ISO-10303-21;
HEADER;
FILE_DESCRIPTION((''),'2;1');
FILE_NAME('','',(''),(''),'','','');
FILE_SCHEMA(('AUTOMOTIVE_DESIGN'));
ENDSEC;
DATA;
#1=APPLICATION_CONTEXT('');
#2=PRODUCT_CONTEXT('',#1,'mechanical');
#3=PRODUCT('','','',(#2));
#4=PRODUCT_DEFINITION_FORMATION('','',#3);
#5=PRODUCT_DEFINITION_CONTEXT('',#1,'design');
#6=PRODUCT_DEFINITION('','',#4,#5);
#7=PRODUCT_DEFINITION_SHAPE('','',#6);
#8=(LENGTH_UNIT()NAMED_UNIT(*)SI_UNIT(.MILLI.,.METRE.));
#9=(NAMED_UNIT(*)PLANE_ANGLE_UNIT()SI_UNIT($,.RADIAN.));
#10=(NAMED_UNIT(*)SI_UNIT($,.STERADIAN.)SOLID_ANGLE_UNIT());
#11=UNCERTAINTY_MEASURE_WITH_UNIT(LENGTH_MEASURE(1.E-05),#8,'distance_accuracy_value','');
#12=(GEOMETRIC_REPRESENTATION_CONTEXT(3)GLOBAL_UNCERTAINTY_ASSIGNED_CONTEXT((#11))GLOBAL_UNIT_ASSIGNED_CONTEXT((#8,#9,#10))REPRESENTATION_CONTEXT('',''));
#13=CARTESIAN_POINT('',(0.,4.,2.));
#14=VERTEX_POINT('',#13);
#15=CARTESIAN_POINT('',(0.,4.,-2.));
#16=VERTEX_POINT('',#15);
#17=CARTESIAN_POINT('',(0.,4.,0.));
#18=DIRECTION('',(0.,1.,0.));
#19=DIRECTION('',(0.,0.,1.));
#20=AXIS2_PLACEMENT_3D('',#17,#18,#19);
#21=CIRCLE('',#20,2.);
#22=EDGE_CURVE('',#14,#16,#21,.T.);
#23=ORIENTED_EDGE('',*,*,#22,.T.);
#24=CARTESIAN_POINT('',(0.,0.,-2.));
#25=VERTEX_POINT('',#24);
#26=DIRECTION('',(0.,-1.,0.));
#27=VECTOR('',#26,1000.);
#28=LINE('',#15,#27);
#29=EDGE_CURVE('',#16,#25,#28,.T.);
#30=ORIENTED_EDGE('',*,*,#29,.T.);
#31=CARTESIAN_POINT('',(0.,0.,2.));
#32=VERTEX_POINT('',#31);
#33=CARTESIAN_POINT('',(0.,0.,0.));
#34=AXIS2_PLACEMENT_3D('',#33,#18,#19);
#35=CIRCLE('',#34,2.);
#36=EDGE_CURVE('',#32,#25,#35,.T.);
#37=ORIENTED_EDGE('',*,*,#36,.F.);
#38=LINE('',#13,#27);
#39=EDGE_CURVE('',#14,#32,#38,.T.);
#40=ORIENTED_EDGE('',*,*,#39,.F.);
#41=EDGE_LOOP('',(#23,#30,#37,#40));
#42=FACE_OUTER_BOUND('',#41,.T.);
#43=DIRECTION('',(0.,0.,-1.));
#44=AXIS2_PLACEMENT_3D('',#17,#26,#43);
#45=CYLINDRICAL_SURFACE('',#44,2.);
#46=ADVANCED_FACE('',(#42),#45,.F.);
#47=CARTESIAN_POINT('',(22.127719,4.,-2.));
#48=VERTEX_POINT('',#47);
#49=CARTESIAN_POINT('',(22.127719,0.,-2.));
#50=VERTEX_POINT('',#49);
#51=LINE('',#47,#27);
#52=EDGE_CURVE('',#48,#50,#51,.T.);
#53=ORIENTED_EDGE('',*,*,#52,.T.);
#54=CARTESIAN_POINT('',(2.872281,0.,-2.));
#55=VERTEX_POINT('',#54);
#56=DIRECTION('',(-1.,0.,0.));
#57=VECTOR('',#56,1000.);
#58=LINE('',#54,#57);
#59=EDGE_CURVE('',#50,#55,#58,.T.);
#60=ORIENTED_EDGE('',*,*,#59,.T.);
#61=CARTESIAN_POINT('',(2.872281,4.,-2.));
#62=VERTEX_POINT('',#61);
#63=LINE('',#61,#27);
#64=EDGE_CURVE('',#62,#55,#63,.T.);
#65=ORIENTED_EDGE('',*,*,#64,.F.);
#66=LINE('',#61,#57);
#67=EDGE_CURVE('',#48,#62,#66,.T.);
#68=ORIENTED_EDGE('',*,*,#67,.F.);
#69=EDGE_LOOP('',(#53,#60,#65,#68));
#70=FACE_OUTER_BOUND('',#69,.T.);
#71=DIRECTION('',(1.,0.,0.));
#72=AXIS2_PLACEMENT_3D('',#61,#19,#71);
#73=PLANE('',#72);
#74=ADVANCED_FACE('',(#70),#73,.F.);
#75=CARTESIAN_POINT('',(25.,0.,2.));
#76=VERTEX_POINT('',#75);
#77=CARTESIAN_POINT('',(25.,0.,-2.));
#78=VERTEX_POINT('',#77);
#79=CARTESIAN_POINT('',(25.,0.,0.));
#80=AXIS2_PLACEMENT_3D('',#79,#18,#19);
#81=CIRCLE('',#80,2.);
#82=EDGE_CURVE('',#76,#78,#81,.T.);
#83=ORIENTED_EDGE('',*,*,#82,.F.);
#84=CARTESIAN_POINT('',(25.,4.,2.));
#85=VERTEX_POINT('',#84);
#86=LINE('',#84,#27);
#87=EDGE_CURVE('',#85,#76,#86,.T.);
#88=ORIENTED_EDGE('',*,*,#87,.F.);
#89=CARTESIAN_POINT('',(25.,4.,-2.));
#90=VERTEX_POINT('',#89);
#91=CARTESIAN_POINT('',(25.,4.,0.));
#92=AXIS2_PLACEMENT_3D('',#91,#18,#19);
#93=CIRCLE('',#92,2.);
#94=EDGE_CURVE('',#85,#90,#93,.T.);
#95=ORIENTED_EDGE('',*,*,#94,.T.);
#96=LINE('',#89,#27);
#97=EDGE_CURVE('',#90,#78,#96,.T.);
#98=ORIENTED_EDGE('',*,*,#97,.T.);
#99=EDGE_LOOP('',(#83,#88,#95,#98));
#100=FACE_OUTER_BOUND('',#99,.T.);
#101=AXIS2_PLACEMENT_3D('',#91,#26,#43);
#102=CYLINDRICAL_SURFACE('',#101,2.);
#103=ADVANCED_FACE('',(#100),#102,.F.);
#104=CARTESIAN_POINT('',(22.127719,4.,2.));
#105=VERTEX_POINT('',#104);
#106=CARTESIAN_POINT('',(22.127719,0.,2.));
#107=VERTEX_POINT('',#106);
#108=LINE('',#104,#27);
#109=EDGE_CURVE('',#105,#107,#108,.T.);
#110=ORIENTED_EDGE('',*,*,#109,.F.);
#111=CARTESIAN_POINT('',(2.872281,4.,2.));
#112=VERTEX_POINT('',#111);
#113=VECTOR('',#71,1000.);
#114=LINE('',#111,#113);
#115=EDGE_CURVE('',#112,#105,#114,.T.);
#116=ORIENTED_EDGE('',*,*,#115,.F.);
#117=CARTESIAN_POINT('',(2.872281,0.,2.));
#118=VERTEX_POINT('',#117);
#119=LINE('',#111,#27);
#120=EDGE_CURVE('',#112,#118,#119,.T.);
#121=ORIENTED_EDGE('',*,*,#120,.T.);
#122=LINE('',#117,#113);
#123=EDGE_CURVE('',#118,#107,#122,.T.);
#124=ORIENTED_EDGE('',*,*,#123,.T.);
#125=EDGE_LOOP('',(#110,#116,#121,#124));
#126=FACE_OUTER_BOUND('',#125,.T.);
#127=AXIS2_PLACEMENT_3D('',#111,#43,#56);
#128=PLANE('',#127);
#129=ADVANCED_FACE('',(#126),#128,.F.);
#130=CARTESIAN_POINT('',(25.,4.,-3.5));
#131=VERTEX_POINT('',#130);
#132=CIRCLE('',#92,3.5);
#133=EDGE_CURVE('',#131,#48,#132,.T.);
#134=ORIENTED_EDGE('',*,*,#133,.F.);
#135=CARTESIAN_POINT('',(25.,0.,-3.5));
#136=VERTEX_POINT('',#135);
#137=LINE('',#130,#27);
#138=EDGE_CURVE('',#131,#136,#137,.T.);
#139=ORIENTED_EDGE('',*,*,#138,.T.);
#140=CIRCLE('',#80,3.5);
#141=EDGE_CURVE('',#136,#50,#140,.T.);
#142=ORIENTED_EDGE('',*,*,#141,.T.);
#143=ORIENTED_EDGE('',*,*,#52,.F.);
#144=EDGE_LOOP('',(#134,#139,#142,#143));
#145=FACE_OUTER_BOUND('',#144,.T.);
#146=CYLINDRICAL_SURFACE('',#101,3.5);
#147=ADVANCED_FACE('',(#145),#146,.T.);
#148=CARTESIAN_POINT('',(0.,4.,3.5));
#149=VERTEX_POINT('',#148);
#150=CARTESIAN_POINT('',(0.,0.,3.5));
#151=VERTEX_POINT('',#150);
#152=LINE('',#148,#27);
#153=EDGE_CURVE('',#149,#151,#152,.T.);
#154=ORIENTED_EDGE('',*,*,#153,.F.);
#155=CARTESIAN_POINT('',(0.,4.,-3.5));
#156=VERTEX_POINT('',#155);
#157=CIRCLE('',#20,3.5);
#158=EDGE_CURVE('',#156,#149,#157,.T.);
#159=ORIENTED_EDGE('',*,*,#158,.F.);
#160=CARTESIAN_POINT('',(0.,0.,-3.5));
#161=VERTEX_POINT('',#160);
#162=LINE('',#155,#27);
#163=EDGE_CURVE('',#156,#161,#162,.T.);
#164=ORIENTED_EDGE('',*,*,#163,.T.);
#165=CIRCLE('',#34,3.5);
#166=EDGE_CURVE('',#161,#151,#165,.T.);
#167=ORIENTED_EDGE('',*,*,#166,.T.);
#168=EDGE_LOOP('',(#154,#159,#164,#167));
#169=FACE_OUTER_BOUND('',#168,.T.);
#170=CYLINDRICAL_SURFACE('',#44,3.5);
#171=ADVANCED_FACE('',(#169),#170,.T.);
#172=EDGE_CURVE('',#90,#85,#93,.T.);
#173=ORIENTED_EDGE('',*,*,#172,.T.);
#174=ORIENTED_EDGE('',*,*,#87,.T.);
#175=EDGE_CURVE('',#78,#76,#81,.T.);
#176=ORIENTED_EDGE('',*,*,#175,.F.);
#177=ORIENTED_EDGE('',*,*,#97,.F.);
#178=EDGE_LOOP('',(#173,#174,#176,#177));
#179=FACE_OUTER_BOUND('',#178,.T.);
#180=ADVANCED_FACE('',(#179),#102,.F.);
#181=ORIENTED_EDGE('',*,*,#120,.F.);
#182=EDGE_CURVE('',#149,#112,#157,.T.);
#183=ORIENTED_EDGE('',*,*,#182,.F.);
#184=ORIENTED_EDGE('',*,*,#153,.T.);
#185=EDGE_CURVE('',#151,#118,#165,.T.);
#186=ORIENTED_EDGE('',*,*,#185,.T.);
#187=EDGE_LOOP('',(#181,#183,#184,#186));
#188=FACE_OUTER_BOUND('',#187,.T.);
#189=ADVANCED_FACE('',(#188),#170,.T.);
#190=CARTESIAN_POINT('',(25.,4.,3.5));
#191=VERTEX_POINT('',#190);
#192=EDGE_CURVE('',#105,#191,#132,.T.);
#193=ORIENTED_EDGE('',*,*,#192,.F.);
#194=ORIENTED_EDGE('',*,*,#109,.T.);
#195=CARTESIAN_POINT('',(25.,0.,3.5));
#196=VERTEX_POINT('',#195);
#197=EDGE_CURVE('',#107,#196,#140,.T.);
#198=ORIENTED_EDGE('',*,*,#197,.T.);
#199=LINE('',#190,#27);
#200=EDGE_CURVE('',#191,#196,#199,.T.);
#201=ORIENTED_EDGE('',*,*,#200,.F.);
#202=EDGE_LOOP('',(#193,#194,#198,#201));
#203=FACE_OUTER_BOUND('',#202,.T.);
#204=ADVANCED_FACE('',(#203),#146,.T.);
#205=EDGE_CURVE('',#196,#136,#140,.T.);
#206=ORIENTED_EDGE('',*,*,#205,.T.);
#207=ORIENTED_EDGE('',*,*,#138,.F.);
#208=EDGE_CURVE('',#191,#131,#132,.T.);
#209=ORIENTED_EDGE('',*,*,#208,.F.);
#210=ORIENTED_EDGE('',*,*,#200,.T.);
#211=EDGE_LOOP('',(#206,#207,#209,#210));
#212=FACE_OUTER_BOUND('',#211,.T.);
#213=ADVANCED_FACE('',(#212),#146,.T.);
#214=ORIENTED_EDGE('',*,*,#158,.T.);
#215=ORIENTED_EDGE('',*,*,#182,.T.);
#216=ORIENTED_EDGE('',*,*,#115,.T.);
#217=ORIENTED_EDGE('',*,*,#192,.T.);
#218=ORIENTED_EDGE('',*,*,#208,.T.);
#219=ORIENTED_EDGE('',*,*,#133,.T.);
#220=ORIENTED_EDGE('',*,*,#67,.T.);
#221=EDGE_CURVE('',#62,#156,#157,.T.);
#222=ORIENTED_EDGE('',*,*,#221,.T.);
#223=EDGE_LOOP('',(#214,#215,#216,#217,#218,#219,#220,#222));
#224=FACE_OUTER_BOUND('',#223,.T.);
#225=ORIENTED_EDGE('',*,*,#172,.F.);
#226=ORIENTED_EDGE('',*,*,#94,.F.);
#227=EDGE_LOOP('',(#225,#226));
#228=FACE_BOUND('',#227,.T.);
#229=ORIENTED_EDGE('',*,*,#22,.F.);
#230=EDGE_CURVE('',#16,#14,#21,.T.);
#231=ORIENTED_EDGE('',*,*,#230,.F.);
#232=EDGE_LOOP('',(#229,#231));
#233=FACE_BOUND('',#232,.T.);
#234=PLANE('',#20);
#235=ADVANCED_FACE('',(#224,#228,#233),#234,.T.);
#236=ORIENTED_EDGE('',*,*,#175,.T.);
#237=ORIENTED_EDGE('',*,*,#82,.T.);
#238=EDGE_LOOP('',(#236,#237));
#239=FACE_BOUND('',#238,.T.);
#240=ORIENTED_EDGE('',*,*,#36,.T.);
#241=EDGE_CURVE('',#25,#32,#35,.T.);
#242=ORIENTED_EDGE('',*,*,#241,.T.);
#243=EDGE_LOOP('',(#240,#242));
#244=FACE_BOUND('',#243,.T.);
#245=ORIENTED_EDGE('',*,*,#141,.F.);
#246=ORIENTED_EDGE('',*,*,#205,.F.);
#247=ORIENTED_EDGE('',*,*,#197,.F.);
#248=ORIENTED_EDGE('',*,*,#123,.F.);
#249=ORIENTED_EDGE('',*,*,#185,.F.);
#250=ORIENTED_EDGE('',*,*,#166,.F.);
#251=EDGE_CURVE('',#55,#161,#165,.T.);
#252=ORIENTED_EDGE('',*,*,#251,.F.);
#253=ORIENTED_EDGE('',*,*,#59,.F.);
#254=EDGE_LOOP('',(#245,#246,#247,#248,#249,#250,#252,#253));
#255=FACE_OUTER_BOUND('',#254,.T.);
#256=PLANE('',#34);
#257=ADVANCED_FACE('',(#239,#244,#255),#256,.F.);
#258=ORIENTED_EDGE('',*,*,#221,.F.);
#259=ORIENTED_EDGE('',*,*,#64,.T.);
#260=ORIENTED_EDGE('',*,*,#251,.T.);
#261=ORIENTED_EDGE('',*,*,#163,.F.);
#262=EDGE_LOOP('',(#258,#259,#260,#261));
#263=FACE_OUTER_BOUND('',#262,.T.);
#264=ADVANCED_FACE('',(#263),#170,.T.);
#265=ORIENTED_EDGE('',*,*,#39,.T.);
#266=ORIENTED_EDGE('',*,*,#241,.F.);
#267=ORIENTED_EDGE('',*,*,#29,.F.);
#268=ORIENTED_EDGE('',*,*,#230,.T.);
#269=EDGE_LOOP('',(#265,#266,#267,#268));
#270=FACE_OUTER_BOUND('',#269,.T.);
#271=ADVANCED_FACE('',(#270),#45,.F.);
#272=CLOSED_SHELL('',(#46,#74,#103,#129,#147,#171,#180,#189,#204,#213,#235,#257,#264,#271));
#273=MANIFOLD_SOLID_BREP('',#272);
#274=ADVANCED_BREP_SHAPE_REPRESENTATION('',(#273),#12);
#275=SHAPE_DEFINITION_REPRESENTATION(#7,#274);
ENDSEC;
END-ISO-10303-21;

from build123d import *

# Parameters (mm, degrees)
SKETCH1_R           = 4
BOSS_EXTRUDE1_DEPTH = 8
SCALE1_SCALE        = 0.5


with BuildPart() as part:
    # Sketch1 → Boss-Extrude1 (new body)
    with BuildSketch(Plane(origin=(0, 0, 0), x_dir=(1, 0, 0), z_dir=(0, 1, 0))):
        with BuildLine():
            Line((5.744562647, 4), (44.255437353, 4))
            ThreePointArc((44.255437353, 4), (57, 0), (44.255437353, -4))
            Line((44.255437353, -4), (5.744562647, -4))
            ThreePointArc((5.744562647, -4), (-7, 0), (5.744562647, 4))
        make_face()
        with Locations(Location((0, 0, 0), (0, 0, 270))):
            Circle(SKETCH1_R, mode=Mode.SUBTRACT)
        with Locations(Location((50, 0, 0), (0, 0, 270))):
            Circle(SKETCH1_R, mode=Mode.SUBTRACT)
    extrude(amount=BOSS_EXTRUDE1_DEPTH)


with BuildPart() as part_1:
    # Scale1: scaled about (0, 0, 0)
    add(part.part.scale(SCALE1_SCALE))


solid = part_1.part
